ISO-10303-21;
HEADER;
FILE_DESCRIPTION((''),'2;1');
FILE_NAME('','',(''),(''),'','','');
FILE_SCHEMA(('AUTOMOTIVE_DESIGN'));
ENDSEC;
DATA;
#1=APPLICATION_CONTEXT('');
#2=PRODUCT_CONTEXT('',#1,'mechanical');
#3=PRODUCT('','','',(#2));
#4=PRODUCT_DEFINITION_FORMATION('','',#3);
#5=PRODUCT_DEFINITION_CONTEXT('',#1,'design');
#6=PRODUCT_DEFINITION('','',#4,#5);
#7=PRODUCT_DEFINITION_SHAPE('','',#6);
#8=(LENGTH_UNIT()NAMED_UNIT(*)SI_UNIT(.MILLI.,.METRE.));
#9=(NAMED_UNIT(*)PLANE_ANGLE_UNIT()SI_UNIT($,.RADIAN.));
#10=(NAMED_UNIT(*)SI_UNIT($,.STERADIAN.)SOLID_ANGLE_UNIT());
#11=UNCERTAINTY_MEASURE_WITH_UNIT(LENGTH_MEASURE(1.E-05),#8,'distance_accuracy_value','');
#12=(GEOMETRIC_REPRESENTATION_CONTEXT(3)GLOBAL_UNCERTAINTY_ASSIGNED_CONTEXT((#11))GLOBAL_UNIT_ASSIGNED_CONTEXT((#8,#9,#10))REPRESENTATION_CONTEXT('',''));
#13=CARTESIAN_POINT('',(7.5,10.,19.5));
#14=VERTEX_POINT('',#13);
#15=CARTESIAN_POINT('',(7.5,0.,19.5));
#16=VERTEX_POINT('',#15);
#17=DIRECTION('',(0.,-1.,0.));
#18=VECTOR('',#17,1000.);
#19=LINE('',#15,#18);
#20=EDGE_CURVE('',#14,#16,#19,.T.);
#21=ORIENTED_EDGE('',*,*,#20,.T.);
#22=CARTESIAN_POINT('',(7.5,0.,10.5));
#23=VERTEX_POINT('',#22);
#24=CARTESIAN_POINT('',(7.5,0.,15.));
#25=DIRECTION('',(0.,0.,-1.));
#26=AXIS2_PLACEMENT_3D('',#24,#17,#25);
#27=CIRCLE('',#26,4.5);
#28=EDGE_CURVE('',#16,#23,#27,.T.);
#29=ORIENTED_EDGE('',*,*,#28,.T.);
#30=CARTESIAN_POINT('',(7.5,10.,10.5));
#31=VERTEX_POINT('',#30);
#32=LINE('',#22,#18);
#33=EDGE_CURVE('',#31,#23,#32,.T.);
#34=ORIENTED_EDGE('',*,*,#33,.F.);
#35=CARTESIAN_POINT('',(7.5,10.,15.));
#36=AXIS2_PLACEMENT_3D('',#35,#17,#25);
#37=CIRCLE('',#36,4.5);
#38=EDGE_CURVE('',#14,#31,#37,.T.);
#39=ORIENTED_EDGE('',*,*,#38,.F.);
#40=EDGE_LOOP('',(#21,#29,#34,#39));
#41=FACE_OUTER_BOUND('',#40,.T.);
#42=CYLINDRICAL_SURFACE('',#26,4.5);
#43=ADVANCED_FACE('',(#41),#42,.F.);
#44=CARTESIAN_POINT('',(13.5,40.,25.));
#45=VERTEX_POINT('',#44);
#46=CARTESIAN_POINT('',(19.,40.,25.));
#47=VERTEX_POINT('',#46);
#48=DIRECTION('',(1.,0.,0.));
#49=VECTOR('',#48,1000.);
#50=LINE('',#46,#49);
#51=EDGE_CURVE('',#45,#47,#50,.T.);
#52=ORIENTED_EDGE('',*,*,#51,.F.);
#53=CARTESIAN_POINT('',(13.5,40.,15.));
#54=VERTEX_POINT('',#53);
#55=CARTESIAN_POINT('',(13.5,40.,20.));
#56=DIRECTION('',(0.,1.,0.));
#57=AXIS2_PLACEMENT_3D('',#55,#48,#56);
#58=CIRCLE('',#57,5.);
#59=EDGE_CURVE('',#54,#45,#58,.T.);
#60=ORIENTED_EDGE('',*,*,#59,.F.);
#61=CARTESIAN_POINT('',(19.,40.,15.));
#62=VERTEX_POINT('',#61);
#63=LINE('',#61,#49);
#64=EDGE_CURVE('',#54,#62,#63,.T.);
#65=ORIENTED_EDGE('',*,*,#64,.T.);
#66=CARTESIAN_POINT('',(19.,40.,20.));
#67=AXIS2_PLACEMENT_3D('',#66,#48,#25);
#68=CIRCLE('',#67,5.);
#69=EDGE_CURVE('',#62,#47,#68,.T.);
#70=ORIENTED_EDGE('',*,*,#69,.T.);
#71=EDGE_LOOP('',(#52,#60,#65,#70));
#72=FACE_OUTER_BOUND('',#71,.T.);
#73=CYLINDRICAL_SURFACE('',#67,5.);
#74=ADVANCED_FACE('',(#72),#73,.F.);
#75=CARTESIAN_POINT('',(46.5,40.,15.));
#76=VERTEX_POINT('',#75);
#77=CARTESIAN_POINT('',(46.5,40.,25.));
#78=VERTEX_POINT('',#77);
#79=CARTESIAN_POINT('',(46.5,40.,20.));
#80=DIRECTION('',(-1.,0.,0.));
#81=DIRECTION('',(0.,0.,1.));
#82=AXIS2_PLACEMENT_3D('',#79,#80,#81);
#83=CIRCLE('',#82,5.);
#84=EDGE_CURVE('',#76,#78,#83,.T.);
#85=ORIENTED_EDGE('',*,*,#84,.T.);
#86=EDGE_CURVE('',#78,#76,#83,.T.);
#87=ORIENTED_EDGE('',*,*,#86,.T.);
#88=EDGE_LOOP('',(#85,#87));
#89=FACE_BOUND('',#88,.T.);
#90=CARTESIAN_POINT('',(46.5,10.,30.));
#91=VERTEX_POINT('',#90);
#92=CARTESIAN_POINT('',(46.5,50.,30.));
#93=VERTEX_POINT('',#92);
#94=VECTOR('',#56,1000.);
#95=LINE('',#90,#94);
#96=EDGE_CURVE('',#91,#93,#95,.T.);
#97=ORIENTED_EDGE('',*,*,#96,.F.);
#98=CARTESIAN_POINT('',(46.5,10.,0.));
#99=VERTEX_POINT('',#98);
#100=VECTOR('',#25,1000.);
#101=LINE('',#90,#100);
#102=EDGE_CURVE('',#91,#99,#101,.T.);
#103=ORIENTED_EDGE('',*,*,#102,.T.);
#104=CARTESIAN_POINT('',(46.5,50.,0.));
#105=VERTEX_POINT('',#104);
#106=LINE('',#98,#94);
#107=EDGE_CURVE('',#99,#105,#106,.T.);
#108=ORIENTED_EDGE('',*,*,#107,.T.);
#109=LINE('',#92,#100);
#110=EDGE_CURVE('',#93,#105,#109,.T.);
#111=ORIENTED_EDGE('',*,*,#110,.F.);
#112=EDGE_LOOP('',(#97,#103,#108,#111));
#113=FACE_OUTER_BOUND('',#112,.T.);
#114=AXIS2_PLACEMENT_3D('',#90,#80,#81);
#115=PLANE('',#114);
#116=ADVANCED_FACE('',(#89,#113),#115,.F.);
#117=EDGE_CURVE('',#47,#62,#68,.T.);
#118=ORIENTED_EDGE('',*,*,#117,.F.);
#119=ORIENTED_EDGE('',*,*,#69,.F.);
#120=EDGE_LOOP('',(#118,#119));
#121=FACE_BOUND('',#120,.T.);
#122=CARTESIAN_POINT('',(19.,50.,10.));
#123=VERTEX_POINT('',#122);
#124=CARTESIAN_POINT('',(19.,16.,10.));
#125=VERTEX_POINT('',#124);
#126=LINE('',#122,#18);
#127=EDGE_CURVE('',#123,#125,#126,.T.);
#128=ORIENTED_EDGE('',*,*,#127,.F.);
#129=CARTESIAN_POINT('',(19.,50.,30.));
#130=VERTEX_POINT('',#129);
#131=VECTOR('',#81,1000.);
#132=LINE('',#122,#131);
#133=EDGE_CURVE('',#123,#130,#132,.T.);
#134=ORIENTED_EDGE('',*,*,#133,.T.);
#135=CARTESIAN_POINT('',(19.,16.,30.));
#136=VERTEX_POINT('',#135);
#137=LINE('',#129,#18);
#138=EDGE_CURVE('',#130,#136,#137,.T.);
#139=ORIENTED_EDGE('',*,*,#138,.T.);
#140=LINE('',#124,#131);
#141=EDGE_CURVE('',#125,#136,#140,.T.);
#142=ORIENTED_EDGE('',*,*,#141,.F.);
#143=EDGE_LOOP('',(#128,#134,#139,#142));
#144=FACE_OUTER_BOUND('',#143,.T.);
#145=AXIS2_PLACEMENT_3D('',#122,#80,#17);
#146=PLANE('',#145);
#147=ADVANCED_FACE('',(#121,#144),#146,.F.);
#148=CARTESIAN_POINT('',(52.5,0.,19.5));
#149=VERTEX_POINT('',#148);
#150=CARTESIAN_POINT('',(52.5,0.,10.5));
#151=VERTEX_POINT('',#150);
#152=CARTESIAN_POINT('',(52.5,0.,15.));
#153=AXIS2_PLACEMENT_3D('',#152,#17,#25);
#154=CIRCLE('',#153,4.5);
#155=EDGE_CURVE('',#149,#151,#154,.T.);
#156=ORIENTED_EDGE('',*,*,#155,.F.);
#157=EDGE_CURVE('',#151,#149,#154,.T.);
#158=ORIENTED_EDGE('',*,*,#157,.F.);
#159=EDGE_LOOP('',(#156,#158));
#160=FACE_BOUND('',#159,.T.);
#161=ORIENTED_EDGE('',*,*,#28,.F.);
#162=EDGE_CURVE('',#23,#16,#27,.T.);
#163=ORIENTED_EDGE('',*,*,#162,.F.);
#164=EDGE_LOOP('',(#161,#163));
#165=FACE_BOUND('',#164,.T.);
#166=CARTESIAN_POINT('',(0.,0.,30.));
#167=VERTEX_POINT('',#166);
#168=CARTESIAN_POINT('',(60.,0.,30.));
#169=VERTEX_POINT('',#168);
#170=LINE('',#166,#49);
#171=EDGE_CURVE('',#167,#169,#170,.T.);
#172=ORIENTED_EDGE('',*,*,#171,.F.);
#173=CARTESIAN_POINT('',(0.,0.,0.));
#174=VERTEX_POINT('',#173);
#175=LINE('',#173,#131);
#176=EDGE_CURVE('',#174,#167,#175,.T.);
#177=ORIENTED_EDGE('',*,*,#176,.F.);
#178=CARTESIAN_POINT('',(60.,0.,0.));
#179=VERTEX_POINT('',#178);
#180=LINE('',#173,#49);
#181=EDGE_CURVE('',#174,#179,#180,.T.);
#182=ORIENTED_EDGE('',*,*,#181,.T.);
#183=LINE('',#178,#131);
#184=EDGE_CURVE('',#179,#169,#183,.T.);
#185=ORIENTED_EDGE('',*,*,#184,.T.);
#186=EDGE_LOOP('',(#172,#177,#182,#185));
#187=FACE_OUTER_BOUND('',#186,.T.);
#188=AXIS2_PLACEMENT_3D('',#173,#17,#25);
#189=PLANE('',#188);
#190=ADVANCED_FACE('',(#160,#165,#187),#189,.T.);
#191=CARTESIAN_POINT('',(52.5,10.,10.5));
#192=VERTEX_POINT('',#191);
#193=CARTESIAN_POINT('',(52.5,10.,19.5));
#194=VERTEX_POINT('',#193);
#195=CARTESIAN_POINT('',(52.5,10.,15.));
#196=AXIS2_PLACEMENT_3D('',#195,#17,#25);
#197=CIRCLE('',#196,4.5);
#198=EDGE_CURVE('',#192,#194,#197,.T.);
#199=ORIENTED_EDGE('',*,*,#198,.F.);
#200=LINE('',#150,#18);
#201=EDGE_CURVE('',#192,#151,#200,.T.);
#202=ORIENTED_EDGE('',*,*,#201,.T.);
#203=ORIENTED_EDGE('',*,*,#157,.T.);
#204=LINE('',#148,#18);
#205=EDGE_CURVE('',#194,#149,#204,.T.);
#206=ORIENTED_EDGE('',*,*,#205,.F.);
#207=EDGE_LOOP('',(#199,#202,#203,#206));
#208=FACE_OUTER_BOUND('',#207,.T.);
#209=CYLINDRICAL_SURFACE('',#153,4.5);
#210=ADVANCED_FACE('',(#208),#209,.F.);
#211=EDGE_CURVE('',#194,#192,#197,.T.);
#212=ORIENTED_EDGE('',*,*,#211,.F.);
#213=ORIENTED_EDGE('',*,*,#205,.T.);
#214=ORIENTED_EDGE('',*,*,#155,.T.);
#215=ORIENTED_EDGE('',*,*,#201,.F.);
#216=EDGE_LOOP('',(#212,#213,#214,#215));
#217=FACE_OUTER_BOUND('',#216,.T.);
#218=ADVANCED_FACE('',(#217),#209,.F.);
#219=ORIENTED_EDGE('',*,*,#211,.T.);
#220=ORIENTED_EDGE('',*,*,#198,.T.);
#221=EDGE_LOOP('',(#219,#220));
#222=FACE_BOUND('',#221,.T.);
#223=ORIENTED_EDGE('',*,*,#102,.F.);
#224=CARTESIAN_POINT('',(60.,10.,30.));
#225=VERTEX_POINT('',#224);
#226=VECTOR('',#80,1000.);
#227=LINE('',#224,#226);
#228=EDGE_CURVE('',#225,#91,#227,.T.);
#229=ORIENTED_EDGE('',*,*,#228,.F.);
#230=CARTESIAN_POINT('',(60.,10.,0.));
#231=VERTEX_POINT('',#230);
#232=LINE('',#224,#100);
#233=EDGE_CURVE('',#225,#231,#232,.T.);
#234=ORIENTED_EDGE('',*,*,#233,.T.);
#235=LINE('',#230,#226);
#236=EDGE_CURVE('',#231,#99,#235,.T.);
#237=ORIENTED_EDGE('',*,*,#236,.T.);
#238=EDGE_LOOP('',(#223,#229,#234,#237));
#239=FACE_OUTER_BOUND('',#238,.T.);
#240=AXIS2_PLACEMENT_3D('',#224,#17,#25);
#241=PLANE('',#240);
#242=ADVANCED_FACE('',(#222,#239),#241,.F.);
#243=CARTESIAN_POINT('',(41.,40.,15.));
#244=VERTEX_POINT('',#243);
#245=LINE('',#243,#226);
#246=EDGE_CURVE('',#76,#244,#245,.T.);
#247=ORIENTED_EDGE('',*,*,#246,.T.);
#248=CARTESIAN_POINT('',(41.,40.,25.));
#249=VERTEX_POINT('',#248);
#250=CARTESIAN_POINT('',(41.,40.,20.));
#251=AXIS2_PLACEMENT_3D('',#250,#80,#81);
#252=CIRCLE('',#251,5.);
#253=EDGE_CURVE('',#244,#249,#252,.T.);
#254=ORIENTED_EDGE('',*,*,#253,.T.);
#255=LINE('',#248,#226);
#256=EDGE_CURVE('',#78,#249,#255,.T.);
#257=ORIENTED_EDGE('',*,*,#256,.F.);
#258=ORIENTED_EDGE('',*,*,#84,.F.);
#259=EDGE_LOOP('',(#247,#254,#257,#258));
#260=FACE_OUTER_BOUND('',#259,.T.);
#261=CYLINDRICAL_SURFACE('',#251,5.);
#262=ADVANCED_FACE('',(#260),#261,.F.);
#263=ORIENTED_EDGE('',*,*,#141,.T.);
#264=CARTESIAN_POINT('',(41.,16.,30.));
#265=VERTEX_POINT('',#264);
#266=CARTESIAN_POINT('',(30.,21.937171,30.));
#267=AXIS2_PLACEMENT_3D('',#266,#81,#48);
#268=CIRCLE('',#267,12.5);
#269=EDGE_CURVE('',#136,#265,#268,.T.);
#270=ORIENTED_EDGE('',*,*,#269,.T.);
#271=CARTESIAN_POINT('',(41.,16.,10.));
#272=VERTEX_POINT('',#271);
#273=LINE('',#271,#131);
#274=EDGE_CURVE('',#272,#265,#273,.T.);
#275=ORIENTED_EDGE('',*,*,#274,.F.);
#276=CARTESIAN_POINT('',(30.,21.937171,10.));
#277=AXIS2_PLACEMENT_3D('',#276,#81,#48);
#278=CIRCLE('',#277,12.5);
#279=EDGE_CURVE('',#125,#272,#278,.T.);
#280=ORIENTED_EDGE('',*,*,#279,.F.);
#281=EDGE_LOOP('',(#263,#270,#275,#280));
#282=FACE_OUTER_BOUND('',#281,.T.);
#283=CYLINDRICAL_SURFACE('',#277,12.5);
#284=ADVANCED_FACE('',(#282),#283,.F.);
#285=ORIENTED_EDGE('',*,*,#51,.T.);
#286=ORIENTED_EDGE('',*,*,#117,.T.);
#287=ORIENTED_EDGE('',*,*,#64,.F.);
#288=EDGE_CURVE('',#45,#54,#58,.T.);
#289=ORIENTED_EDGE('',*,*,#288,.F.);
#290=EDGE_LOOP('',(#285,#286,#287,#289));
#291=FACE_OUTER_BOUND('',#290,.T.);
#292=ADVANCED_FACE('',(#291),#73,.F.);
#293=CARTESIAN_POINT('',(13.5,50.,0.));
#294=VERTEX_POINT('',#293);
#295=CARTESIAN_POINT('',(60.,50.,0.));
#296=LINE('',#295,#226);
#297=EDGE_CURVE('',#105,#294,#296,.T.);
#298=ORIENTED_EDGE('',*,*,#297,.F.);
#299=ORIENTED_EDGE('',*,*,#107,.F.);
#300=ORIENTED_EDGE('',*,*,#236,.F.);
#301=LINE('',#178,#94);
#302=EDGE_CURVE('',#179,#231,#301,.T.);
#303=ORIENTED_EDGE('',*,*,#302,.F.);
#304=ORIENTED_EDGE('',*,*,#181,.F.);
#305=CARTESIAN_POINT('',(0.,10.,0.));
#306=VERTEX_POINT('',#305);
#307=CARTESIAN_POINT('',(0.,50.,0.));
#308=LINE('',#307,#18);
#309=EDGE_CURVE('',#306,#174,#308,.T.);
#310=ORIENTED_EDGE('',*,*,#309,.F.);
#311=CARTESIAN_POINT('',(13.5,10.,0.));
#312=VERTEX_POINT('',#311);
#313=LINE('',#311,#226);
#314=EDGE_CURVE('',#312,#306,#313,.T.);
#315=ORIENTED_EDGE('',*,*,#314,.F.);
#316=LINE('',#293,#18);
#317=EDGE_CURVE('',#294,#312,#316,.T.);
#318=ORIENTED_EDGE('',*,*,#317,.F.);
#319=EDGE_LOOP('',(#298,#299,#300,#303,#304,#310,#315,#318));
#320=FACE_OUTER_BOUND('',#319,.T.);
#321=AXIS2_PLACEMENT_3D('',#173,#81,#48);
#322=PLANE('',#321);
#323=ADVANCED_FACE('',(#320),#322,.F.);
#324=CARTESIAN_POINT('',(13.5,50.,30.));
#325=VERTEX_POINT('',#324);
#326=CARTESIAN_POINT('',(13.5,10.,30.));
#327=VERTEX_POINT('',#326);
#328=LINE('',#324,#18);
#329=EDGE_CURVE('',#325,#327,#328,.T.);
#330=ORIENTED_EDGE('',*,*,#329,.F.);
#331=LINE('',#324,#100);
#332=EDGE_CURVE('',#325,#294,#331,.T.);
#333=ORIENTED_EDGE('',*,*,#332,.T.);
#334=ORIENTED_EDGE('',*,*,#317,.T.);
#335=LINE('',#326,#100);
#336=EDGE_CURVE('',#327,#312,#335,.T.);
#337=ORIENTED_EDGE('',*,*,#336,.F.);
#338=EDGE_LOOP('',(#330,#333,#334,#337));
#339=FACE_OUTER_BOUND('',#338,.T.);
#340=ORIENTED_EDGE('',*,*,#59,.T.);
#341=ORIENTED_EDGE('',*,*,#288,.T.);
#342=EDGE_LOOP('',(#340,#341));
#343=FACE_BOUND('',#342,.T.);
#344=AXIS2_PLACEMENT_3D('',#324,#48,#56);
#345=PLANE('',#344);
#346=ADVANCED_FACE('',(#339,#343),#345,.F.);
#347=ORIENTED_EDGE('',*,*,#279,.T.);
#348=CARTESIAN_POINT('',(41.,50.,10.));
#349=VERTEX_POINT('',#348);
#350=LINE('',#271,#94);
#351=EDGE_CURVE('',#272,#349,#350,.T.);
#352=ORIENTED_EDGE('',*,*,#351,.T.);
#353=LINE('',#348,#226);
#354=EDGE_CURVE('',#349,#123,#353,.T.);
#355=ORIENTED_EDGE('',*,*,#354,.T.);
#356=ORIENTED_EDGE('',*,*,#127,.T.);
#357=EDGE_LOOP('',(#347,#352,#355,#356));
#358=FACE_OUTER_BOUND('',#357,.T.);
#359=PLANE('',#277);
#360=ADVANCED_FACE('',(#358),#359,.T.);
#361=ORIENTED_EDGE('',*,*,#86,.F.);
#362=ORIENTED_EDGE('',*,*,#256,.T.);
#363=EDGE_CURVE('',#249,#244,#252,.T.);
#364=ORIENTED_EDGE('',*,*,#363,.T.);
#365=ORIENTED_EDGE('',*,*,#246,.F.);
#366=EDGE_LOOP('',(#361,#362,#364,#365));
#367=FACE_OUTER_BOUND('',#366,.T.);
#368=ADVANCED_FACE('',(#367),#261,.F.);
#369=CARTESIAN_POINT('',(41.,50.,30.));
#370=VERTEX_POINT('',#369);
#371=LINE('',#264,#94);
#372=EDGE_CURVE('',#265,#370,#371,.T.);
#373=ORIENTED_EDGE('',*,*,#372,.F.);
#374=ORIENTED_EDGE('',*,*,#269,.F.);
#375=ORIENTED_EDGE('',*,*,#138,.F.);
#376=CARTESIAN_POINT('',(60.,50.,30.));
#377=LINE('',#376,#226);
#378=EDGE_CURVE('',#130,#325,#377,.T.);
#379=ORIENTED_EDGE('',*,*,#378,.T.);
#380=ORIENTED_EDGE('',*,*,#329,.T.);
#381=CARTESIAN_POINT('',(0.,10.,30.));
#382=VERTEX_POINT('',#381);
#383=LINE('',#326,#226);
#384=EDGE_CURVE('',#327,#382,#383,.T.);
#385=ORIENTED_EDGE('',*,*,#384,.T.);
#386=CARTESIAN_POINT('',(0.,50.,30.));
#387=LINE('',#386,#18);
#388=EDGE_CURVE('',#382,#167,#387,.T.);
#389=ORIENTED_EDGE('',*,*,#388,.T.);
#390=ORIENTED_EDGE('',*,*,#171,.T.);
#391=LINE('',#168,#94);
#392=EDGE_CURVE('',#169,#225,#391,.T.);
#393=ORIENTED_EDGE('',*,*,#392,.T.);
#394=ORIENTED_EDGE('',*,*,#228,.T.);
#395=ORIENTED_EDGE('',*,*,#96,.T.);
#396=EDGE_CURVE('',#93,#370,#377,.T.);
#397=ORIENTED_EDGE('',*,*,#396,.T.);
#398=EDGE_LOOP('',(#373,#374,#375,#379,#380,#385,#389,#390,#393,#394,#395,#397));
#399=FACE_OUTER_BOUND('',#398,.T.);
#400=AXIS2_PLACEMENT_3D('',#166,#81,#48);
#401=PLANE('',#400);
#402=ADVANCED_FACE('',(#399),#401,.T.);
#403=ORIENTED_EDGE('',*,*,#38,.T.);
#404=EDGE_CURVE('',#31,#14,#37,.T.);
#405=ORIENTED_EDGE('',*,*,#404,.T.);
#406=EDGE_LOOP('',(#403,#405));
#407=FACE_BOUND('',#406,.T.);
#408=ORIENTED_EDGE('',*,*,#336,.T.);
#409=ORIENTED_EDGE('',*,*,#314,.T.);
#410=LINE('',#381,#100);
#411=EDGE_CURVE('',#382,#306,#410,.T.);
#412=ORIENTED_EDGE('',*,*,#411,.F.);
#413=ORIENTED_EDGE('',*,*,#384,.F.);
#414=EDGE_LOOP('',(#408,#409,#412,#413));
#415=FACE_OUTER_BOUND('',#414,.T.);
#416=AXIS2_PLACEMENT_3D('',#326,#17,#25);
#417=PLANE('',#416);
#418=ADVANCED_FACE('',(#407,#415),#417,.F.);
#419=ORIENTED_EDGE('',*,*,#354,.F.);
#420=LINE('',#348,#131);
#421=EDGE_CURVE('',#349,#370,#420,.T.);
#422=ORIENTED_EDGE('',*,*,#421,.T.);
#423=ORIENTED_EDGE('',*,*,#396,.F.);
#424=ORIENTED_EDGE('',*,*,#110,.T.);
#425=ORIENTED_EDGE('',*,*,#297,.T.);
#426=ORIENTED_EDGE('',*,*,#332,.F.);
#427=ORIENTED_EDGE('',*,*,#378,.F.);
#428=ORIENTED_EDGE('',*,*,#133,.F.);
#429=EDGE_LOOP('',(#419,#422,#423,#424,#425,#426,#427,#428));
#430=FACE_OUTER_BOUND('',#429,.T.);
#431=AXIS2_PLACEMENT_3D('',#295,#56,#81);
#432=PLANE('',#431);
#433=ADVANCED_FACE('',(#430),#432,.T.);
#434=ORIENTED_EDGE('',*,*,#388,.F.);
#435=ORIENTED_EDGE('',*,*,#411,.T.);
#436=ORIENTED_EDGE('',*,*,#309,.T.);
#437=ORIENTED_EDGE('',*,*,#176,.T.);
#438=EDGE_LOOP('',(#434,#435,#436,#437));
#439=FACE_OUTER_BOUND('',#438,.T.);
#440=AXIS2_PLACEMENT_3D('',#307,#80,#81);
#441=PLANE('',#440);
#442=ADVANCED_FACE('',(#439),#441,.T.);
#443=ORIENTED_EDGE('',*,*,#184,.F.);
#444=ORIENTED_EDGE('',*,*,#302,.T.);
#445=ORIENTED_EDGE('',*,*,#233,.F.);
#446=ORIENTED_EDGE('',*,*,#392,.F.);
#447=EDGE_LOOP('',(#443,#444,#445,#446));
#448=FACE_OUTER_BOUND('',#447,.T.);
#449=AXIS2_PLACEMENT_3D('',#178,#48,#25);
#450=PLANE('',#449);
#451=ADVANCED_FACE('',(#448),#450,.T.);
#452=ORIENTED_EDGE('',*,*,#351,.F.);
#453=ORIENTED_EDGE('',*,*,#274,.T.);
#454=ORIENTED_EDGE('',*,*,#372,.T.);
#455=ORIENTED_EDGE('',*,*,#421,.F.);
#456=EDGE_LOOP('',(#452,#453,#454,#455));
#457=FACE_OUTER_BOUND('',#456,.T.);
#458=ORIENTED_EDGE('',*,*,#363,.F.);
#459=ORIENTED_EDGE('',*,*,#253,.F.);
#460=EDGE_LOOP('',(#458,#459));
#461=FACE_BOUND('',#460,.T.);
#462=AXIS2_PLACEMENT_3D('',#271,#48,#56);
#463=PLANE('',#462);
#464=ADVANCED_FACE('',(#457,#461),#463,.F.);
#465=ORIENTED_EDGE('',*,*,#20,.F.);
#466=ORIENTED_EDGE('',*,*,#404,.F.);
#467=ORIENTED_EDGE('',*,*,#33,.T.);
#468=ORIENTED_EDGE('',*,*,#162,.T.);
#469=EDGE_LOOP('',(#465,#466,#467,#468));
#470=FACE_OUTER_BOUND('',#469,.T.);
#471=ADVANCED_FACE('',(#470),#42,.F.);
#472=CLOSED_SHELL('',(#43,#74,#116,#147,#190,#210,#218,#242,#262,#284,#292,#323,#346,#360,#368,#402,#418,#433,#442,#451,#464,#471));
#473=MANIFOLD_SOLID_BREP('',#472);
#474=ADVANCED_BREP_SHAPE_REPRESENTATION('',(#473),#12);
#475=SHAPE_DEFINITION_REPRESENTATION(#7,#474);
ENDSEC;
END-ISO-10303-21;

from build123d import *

# Parameters (mm, degrees)
SKETCH1_W                      = 60
SKETCH1_H                      = 50
BOSS_EXTRUDE1_DEPTH            = 30
SKETCH2_W                      = 13.5
SKETCH2_H                      = 40
CUT_EXTRUDE1_DEPTH             = 84.666002653
SKETCH3_W                      = 13.5
SKETCH3_H                      = 40
CUT_EXTRUDE2_DEPTH             = 84.666002653
CUT_EXTRUDE3_DEPTH             = 20
F_9_0_9_DIAMETER_HOLE1_D       = 9
F_10_0_10_DIAMETER_HOLE1_D     = 10
F_10_0_10_DIAMETER_HOLE1_DEPTH = 19
F_10_0_10_DIAMETER_HOLE2_D     = 10
F_10_0_10_DIAMETER_HOLE2_DEPTH = 19


with BuildPart() as part:
    # Sketch1 → Boss-Extrude1 (new body)
    with BuildSketch(Plane.XY.offset(30)):
        with Locations((30, 25)):
            Rectangle(SKETCH1_W, SKETCH1_H)
    extrude(amount=-BOSS_EXTRUDE1_DEPTH)

    # Sketch2 → Cut-Extrude1 (cut, through all)
    with BuildSketch(Plane(origin=(0, 0, 0), x_dir=(-1, 0, 0), z_dir=(0, 0, -1))):
        with Locations((-53.25, 30)):
            Rectangle(SKETCH2_W, SKETCH2_H)
    extrude(amount=-CUT_EXTRUDE1_DEPTH, mode=Mode.SUBTRACT)

    # Sketch3 → Cut-Extrude2 (cut, through all)
    with BuildSketch(Plane(origin=(0, 0, 0), x_dir=(-1, 0, 0), z_dir=(0, 0, -1))):
        with Locations((-6.75, 30)):
            Rectangle(SKETCH3_W, SKETCH3_H)
    extrude(amount=-CUT_EXTRUDE2_DEPTH, mode=Mode.SUBTRACT)

    # Sketch4 → Cut-Extrude3 (cut)
    with BuildSketch(Plane.XY.offset(30)):
        with BuildLine():
            Line((19, 50), (19, 16))
            ThreePointArc((19, 16), (30, 9.437171044), (41, 16))
            Line((41, 16), (41, 50))
            Line((41, 50), (19, 50))
        make_face()
    extrude(amount=-CUT_EXTRUDE3_DEPTH, mode=Mode.SUBTRACT)

    # Ø9.0 (9) Diameter Hole1 (through all)
    with Locations(Plane(origin=(0, 0, 0), x_dir=(-1, 0, 0), z_dir=(0, -1, 0))):
        with Locations((-7.5, -15), (-52.5, -15)):
            Hole(F_9_0_9_DIAMETER_HOLE1_D / 2)

    # Ø10.0 (10) Diameter Hole1
    with Locations(Plane.ZY.offset(-41)):
        with Locations((20, 40)):
            Hole(F_10_0_10_DIAMETER_HOLE1_D / 2, depth=F_10_0_10_DIAMETER_HOLE1_DEPTH)

    # Ø10.0 (10) Diameter Hole2
    with Locations(Plane(origin=(19, 0, 0), x_dir=(0, 0, -1), z_dir=(1, 0, 0))):
        with Locations((-20, 40)):
            Hole(F_10_0_10_DIAMETER_HOLE2_D / 2, depth=F_10_0_10_DIAMETER_HOLE2_DEPTH)


solid = part.part
